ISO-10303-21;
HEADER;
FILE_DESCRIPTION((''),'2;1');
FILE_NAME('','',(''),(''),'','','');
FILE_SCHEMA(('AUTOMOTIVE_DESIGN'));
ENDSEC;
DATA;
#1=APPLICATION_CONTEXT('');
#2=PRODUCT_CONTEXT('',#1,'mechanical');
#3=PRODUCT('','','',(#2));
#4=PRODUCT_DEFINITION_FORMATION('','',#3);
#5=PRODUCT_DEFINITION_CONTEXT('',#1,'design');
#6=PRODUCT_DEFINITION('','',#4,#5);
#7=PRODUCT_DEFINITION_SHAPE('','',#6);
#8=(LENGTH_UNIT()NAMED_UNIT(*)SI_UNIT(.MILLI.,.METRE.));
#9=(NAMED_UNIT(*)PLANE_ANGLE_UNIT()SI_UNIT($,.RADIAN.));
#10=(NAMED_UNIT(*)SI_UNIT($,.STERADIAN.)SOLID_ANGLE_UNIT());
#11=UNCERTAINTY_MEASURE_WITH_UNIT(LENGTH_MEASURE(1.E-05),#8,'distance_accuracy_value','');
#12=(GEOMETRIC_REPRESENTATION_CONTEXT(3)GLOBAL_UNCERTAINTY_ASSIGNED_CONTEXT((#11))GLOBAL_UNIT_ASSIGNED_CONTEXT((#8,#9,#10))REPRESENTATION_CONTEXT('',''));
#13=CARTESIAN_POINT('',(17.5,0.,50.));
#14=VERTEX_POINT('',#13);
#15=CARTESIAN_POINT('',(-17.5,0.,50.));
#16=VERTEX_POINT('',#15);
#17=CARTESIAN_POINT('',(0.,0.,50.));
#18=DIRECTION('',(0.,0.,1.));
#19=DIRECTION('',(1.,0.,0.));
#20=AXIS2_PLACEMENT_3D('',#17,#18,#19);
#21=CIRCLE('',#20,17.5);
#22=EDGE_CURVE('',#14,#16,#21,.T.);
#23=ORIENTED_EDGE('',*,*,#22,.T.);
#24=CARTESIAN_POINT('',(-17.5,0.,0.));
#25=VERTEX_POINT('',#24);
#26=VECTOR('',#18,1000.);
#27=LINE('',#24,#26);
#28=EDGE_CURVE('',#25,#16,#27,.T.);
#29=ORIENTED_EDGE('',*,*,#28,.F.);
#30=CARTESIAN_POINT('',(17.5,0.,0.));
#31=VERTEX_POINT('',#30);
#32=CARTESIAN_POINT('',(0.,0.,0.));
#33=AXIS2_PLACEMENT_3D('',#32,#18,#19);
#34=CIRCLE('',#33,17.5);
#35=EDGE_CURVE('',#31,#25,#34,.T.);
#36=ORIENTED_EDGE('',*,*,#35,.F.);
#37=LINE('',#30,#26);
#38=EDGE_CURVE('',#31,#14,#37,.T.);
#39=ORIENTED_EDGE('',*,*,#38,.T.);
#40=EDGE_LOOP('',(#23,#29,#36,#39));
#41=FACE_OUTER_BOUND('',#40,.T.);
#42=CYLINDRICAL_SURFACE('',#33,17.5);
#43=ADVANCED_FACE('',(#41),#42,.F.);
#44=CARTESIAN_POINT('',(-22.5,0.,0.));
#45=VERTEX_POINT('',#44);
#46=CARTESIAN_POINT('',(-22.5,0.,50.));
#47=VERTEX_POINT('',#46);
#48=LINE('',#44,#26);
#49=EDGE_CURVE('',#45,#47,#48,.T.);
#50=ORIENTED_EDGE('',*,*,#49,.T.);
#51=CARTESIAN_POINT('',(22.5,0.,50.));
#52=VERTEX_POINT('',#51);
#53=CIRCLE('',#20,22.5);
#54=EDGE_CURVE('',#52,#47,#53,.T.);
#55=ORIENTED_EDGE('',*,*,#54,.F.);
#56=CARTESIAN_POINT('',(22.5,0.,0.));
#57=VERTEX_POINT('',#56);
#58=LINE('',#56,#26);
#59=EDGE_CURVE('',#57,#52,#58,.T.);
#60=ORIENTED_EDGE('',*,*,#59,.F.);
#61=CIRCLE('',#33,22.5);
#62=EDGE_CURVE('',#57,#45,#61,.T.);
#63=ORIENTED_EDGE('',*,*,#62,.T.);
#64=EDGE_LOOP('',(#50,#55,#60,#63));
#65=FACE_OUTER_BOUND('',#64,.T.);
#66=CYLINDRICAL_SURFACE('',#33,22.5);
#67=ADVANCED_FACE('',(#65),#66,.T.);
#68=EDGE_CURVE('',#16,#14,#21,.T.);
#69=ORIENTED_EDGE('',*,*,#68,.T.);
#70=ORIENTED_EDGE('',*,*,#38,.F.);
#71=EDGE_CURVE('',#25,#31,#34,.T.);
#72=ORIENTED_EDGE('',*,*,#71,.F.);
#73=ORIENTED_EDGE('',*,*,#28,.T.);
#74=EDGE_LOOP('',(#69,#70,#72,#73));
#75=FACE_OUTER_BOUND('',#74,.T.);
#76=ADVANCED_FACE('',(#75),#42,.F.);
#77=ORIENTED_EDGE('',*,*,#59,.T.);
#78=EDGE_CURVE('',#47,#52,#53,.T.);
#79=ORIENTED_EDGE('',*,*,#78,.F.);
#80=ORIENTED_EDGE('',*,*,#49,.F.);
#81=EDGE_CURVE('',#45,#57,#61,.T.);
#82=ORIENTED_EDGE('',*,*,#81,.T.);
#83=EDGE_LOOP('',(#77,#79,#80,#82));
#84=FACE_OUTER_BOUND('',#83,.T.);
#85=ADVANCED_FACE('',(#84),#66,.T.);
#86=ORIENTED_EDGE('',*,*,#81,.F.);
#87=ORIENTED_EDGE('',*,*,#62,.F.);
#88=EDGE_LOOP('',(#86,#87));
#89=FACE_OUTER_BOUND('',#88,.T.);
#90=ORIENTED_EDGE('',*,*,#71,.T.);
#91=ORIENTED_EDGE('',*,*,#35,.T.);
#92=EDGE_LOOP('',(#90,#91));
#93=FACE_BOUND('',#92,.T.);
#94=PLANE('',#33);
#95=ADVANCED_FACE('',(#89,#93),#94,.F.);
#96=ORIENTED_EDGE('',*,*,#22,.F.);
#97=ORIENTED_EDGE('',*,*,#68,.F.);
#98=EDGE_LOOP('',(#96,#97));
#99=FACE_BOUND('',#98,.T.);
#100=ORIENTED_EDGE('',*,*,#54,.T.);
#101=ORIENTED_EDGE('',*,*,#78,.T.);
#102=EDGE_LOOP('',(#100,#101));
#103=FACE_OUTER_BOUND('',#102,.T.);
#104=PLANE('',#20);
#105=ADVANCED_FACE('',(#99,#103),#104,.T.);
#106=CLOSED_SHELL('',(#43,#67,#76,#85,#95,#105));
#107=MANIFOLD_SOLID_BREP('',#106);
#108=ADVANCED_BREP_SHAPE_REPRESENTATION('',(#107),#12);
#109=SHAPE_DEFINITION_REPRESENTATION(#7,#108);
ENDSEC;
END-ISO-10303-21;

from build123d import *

# Parameters (mm, degrees)
SKETCH_1_R          = 20
SKETCH_1_R_2        = 15
EXTRUDE_1_DEPTH     = 50
EXTRUDE_START       = -50
SKETCH_2_R          = 22.5
SKETCH_2_R_2        = 20
EXTRUDE_2_DEPTH     = 50
SKETCH_3_R          = 17.5
CUT_EXTRUDE_2_DEPTH = 50


with BuildPart() as part:
    # 草图1 → 凸台-拉伸1 (new body)
    with BuildSketch(Plane.XY):
        Circle(SKETCH_1_R)
        Circle(SKETCH_1_R_2, mode=Mode.SUBTRACT)
    extrude(amount=EXTRUDE_1_DEPTH)

    # 草图2 → 凸台-拉伸2 (add)
    with BuildSketch(Plane.XY.offset(50).offset(EXTRUDE_START)):
        Circle(SKETCH_2_R)
        Circle(SKETCH_2_R_2, mode=Mode.SUBTRACT)
    extrude(amount=EXTRUDE_2_DEPTH)

    # 草图3 → 切除-拉伸2 (cut)
    with BuildSketch(Plane.XY.offset(50)):
        Circle(SKETCH_3_R)
    extrude(amount=-CUT_EXTRUDE_2_DEPTH, mode=Mode.SUBTRACT)


solid = part.part
